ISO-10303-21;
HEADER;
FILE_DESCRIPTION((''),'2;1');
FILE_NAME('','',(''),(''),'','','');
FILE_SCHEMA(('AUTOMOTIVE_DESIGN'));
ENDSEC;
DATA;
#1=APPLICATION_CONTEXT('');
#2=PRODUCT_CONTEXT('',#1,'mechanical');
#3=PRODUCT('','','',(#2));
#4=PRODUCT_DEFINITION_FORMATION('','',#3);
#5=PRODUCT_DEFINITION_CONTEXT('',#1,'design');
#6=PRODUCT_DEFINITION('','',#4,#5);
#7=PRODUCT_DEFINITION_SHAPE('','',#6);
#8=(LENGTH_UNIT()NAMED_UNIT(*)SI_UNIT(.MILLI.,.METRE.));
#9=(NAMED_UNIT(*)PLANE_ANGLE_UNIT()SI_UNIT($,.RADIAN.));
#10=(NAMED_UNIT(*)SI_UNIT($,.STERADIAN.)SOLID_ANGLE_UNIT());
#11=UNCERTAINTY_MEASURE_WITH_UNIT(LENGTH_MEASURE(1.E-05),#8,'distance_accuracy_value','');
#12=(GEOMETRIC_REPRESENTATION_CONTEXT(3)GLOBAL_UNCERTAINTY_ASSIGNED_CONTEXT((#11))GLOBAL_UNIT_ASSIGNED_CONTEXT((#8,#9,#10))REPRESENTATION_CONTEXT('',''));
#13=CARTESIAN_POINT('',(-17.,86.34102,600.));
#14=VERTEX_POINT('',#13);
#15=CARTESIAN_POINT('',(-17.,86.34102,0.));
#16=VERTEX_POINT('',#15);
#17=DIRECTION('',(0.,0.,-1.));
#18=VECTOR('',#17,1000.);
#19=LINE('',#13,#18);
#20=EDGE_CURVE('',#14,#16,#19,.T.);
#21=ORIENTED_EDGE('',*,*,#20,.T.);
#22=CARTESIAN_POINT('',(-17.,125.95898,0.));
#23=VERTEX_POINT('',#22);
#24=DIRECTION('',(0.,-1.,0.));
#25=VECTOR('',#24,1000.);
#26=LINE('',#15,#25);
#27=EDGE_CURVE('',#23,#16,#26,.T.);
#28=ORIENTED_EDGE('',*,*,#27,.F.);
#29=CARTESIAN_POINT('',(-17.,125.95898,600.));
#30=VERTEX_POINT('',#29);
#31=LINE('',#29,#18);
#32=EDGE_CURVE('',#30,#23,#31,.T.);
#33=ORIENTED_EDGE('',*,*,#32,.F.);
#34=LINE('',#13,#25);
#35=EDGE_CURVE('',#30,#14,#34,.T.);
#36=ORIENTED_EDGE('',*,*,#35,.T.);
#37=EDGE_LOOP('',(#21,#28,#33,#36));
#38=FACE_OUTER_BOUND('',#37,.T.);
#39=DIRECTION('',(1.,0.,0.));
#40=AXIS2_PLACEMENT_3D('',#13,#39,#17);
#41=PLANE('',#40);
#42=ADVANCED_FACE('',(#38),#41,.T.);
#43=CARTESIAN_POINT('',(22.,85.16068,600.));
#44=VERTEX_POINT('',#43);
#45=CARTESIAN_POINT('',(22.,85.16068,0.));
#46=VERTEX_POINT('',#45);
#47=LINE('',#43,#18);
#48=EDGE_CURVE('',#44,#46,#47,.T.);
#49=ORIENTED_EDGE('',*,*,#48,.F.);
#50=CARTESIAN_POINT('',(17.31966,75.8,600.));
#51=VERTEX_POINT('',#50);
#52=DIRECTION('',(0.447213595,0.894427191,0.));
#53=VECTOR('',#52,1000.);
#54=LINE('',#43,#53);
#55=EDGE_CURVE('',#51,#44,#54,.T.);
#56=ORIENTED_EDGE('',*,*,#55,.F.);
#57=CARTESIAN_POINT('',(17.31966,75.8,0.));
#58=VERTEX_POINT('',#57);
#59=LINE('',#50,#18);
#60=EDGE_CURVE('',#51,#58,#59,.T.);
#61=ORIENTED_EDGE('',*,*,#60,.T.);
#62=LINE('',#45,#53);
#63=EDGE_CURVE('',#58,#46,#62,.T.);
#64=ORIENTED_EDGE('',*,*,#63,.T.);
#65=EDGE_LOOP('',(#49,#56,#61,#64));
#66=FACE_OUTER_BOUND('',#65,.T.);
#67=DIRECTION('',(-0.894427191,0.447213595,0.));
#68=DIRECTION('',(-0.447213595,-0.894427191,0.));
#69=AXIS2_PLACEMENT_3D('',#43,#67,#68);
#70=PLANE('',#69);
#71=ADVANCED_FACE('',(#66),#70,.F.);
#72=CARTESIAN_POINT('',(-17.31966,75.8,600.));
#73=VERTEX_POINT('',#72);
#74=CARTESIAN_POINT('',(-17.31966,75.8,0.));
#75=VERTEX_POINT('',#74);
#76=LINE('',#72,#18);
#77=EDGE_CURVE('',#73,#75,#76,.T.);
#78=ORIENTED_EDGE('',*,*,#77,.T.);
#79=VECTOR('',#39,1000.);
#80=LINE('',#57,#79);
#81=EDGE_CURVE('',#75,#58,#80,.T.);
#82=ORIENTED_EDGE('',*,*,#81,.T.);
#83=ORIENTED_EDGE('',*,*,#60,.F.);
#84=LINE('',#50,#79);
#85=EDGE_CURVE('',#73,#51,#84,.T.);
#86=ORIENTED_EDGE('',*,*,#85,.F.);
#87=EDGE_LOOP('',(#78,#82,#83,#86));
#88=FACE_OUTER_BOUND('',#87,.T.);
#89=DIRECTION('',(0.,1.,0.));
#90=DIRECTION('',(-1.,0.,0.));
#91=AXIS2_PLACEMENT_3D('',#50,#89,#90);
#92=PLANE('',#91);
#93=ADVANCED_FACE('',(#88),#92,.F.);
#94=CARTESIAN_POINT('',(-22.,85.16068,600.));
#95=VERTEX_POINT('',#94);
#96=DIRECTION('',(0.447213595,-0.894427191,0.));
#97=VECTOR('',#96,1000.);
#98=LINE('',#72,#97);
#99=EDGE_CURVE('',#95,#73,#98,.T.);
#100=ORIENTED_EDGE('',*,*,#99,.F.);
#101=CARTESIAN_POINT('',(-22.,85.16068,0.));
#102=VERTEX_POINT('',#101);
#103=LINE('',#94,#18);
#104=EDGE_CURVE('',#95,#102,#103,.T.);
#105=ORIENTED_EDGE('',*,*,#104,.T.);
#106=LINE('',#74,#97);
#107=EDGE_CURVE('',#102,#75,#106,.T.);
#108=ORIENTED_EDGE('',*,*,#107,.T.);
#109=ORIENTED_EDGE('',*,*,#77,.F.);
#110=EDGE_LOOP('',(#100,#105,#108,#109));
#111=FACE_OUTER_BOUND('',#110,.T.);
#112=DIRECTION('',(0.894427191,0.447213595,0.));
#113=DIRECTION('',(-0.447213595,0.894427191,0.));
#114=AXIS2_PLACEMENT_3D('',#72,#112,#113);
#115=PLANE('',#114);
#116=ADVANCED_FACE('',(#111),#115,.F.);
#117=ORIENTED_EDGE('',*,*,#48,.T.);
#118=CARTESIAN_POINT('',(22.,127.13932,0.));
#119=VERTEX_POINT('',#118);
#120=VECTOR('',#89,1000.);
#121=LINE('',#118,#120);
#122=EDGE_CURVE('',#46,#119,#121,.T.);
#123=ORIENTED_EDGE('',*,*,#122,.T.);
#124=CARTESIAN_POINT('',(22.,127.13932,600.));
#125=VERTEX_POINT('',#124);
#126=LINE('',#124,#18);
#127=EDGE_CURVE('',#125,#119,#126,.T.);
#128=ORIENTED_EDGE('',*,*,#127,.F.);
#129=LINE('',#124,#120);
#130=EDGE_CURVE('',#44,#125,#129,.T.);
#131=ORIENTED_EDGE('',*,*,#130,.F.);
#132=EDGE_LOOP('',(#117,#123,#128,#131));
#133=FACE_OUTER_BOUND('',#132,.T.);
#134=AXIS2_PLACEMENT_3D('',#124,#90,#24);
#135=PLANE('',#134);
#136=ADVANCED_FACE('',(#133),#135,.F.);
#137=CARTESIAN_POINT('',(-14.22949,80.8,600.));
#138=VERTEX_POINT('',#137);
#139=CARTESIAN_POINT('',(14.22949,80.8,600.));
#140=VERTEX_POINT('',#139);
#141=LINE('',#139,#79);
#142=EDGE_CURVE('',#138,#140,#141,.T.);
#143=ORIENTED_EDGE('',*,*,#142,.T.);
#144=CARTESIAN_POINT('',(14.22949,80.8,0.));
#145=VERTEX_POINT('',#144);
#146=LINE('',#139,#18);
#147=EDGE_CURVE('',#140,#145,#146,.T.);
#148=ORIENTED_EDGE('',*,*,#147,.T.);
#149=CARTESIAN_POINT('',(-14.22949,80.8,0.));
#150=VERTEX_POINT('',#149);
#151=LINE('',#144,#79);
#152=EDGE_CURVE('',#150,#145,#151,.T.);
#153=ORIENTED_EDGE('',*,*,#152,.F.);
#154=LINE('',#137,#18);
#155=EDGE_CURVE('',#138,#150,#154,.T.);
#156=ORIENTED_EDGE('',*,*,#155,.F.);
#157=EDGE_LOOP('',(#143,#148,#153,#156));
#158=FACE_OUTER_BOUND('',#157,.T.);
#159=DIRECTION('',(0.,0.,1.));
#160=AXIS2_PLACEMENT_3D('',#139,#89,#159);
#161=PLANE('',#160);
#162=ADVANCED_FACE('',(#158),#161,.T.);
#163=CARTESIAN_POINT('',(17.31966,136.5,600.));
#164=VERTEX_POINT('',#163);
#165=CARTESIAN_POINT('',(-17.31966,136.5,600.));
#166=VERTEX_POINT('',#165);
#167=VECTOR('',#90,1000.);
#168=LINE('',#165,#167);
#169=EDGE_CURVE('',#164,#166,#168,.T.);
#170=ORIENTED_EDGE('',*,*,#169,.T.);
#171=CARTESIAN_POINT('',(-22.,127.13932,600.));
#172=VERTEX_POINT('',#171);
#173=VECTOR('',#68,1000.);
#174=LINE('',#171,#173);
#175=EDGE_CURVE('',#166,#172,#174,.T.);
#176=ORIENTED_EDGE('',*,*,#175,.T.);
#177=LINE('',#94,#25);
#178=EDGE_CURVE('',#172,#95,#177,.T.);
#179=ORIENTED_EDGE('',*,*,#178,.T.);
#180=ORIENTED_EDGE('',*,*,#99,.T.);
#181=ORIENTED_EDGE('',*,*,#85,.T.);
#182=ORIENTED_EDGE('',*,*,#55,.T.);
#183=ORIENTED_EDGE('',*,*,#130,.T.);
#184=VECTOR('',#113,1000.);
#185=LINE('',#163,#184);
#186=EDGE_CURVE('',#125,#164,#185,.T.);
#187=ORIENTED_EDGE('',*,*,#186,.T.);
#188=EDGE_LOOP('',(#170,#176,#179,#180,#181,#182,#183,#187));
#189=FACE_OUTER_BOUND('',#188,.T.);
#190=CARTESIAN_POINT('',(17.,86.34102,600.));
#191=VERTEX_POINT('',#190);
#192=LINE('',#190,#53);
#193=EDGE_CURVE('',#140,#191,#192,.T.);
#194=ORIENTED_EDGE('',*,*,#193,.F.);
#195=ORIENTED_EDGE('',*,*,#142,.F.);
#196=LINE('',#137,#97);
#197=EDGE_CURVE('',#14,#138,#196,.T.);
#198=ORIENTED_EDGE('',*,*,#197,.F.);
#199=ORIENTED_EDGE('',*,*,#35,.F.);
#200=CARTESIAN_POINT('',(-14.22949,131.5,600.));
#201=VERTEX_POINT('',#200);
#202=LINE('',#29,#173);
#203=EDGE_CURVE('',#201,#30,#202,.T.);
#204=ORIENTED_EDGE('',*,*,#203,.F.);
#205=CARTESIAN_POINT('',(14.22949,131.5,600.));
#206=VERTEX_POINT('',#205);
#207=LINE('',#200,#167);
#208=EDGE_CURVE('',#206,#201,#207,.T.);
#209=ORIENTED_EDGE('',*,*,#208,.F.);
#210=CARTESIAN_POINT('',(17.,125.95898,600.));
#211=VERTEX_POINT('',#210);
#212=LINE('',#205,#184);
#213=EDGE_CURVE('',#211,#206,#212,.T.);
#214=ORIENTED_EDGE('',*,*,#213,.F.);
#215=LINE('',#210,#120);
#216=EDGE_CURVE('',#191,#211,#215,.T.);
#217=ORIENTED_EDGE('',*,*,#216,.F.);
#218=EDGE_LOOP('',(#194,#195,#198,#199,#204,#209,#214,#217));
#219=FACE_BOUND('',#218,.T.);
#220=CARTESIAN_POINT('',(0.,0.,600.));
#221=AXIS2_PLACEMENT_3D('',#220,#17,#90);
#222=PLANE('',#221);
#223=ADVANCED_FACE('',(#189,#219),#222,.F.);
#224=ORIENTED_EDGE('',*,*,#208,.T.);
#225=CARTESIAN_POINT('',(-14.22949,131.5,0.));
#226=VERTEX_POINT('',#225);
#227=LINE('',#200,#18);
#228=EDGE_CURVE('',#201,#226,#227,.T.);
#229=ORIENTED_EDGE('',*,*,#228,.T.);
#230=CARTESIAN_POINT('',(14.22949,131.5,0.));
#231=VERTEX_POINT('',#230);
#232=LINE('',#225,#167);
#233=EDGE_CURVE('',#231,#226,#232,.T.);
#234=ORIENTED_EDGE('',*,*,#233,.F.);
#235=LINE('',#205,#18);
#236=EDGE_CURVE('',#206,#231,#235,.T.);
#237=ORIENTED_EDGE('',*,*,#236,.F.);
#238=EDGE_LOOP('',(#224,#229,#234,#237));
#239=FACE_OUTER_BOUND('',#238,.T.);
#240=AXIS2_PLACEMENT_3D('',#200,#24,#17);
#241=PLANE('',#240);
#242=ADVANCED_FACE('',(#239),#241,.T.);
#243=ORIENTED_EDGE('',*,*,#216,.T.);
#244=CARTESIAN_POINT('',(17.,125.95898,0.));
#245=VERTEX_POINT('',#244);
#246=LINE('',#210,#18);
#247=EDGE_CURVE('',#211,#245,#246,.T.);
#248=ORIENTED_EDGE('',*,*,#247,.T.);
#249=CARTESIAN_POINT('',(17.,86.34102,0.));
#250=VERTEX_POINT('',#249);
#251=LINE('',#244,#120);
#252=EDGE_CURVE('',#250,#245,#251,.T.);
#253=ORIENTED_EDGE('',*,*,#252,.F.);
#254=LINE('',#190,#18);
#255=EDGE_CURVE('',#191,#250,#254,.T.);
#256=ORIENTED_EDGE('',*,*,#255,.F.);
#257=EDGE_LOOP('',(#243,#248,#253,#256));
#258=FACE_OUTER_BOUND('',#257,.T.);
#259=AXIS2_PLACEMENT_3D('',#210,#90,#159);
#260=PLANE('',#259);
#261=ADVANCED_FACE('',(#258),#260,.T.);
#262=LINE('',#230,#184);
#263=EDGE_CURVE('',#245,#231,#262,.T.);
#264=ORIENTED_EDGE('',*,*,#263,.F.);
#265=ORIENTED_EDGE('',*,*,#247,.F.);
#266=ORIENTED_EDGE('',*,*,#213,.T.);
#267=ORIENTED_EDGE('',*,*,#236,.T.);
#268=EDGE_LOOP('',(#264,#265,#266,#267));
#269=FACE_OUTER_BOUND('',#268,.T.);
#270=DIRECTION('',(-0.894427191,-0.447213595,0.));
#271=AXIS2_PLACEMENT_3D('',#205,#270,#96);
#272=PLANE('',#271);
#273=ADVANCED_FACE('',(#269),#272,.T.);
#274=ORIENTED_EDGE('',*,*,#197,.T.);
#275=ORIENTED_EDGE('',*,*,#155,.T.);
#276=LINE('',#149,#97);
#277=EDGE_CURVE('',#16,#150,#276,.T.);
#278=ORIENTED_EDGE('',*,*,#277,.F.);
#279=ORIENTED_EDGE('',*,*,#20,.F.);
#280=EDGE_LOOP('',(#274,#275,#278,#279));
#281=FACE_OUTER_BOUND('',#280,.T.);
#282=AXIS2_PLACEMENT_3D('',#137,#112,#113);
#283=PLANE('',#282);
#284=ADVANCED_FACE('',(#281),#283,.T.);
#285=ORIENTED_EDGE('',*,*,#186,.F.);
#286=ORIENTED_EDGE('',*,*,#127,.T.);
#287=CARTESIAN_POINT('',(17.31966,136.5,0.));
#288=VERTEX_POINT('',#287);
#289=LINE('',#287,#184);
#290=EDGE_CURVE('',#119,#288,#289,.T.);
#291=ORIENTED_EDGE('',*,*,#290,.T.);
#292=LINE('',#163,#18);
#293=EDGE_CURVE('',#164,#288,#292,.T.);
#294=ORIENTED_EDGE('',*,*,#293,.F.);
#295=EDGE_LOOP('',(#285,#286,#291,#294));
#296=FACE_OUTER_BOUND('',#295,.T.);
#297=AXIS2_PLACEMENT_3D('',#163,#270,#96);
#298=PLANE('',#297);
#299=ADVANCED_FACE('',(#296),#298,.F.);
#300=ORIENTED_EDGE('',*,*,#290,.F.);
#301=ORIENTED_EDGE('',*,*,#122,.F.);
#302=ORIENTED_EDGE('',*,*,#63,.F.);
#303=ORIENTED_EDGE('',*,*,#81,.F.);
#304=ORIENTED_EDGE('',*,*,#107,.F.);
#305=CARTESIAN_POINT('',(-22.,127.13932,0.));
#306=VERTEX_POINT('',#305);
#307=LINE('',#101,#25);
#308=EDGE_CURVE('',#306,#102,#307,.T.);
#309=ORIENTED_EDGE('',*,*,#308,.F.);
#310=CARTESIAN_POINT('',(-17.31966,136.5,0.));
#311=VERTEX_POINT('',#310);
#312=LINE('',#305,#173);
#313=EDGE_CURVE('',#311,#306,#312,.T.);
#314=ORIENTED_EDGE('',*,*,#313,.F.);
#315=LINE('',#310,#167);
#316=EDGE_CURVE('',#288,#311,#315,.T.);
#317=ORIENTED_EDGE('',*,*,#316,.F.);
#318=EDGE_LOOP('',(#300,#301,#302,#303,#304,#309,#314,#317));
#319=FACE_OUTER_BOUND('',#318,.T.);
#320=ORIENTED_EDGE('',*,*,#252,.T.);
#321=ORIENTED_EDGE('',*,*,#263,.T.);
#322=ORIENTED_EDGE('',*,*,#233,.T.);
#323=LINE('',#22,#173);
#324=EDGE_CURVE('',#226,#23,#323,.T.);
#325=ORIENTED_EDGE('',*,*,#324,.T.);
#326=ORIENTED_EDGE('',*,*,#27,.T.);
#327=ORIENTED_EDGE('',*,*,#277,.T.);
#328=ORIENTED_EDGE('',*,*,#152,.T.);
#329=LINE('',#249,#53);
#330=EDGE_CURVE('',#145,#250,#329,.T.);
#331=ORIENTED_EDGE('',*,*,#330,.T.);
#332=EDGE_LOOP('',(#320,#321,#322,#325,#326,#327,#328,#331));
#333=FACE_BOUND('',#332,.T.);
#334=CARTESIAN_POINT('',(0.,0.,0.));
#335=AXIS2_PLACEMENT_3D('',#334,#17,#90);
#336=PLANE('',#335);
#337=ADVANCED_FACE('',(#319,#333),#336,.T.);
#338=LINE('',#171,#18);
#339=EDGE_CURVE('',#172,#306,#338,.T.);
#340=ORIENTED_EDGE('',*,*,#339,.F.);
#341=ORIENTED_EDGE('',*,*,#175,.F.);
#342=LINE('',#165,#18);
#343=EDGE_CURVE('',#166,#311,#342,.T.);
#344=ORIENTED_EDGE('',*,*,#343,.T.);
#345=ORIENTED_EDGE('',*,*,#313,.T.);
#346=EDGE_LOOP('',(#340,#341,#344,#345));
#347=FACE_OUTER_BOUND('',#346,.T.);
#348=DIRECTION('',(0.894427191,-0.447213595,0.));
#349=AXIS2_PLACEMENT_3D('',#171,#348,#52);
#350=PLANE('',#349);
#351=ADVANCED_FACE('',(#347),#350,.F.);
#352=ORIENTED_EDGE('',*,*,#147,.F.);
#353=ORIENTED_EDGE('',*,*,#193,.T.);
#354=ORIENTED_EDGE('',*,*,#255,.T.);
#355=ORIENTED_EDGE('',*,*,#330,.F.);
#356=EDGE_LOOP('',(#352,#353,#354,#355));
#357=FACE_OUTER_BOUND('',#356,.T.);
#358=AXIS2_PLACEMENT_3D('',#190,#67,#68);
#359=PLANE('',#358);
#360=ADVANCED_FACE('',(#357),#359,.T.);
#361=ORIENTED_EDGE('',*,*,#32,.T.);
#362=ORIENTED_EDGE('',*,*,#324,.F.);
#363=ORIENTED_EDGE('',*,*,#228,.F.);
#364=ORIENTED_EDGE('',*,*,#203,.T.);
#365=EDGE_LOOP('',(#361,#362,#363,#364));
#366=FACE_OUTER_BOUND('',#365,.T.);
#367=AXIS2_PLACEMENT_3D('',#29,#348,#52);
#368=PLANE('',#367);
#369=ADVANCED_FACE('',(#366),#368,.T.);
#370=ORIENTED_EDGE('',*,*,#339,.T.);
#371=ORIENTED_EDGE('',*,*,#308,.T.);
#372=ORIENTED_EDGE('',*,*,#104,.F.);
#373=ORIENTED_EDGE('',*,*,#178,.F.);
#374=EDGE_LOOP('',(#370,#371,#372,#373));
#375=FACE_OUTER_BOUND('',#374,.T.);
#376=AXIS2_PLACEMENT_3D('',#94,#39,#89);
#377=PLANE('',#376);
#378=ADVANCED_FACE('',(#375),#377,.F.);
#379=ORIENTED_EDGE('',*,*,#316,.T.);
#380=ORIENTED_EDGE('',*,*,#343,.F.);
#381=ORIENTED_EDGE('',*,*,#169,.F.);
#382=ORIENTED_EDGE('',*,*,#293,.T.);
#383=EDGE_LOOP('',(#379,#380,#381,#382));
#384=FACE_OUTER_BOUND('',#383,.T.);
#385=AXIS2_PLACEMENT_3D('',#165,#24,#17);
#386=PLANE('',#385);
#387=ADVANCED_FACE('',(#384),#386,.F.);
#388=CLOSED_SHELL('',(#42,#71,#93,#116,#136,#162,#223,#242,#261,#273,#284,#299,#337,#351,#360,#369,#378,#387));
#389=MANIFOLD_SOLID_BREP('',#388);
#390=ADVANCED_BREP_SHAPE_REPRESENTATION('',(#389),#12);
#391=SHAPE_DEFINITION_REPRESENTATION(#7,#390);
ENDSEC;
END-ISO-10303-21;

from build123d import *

# Parameters (mm, degrees)
BOSS_EXTRUDE1_DEPTH = 600


with BuildPart() as part:
    # Sketch1 → Boss-Extrude1 (new body)
    with BuildSketch(Plane.XY):
        Polygon((-17.319660113, 136.5), (17.319660113, 136.5), (22, 127.139320225), (22, 85.160679775), (17.319660113, 75.8), (-17.319660113, 75.8), (-22, 85.160679775), (-22, 127.139320225), align=None)
        Polygon((-14.229490169, 131.5), (14.229490169, 131.5), (17, 125.958980338), (17, 86.341019662), (14.229490169, 80.8), (-14.229490169, 80.8), (-17, 86.341019662), (-17, 125.958980338), align=None, mode=Mode.SUBTRACT)
    extrude(amount=BOSS_EXTRUDE1_DEPTH)


solid = part.part
